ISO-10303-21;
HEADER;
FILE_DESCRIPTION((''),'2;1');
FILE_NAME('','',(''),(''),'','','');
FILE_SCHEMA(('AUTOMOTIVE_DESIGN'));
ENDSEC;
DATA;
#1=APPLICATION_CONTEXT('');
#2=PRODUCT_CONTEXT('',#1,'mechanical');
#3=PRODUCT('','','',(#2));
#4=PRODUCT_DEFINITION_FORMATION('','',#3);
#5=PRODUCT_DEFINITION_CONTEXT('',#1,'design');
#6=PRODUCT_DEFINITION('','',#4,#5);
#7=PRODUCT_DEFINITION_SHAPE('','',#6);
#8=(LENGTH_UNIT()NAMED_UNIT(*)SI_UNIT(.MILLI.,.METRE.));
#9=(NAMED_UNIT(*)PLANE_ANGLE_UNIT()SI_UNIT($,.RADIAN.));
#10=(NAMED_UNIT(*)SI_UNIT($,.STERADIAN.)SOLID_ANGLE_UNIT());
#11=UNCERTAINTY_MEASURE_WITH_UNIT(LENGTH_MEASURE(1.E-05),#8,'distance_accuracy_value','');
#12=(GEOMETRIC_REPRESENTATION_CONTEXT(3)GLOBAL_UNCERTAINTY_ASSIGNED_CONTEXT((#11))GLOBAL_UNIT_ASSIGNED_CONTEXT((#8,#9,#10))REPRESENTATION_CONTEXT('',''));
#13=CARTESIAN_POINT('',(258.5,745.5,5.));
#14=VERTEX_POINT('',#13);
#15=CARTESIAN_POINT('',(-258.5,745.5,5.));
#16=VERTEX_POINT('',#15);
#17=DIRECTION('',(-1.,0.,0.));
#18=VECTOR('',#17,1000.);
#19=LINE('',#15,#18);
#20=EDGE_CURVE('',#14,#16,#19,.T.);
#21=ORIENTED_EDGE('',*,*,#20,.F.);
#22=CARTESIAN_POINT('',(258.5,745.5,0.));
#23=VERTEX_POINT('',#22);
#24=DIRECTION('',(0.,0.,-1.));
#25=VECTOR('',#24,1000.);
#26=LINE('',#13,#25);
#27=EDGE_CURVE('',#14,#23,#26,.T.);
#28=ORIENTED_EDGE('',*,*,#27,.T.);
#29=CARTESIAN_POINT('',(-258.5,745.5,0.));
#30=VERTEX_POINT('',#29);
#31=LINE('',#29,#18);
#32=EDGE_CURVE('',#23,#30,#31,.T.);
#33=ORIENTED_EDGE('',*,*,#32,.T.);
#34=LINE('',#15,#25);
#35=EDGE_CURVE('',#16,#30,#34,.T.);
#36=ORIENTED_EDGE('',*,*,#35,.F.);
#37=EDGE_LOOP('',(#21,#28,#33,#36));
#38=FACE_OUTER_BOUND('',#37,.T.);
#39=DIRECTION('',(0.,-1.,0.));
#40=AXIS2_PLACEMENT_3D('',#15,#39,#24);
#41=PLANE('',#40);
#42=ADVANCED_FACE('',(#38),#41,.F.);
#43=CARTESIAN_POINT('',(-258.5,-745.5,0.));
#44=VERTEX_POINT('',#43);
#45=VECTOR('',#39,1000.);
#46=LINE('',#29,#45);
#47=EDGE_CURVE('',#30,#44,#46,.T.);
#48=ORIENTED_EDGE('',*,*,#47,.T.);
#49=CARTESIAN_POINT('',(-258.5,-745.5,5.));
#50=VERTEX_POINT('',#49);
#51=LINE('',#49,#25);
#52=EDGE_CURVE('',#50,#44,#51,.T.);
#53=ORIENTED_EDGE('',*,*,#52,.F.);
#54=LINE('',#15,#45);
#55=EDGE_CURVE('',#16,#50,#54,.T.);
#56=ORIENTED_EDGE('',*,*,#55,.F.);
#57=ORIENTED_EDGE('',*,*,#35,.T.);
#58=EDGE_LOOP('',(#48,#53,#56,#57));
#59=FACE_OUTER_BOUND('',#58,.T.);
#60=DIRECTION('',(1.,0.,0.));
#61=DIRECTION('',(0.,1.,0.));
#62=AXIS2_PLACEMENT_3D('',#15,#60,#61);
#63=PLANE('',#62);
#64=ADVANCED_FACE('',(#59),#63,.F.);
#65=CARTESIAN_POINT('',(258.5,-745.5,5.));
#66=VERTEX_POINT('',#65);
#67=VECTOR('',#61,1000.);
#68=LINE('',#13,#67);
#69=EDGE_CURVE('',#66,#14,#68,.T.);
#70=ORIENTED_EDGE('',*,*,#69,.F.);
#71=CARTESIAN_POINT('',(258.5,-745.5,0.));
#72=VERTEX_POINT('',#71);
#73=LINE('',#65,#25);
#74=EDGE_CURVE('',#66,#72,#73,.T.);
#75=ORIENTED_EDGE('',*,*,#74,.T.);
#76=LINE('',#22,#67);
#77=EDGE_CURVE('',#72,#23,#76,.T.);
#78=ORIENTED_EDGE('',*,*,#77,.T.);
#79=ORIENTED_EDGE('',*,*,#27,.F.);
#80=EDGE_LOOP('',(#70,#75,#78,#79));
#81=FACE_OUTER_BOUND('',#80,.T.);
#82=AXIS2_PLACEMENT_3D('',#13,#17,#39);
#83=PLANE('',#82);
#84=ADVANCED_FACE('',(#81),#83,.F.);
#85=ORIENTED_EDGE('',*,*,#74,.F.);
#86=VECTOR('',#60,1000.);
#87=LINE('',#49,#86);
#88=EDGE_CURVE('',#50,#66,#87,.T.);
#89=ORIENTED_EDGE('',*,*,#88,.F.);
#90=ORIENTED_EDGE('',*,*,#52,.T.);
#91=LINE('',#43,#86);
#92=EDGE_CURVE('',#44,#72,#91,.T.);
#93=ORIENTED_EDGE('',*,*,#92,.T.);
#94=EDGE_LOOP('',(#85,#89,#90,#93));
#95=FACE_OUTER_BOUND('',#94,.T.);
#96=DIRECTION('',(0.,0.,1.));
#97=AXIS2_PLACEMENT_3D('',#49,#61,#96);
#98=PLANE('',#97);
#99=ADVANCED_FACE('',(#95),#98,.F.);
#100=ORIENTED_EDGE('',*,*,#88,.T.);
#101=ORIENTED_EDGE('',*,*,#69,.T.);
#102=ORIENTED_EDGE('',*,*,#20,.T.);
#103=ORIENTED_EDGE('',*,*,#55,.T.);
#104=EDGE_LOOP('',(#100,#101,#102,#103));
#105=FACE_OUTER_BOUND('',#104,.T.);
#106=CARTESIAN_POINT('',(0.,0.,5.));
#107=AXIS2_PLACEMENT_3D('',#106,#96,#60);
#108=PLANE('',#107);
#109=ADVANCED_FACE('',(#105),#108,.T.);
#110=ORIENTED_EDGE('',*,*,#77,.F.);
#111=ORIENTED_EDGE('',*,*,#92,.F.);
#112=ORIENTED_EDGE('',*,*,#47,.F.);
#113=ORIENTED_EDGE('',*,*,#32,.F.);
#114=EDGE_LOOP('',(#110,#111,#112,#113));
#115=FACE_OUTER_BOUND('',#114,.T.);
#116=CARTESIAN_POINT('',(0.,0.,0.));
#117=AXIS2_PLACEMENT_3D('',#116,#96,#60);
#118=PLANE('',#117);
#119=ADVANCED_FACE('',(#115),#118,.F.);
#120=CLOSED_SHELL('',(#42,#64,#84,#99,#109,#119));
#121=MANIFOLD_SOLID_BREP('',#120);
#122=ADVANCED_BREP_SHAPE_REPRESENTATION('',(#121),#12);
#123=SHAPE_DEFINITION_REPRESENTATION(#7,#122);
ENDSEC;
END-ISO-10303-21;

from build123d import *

# Parameters (mm, degrees)
SKETCH_1_W      = 517
SKETCH_1_H      = 1491
EXTRUDE_1_DEPTH = 5


with BuildPart() as part:
    # 草图1 → 凸台-拉伸1 (new body)
    with BuildSketch(Plane.XY):
        Rectangle(SKETCH_1_W, SKETCH_1_H)
    extrude(amount=EXTRUDE_1_DEPTH)


solid = part.part
